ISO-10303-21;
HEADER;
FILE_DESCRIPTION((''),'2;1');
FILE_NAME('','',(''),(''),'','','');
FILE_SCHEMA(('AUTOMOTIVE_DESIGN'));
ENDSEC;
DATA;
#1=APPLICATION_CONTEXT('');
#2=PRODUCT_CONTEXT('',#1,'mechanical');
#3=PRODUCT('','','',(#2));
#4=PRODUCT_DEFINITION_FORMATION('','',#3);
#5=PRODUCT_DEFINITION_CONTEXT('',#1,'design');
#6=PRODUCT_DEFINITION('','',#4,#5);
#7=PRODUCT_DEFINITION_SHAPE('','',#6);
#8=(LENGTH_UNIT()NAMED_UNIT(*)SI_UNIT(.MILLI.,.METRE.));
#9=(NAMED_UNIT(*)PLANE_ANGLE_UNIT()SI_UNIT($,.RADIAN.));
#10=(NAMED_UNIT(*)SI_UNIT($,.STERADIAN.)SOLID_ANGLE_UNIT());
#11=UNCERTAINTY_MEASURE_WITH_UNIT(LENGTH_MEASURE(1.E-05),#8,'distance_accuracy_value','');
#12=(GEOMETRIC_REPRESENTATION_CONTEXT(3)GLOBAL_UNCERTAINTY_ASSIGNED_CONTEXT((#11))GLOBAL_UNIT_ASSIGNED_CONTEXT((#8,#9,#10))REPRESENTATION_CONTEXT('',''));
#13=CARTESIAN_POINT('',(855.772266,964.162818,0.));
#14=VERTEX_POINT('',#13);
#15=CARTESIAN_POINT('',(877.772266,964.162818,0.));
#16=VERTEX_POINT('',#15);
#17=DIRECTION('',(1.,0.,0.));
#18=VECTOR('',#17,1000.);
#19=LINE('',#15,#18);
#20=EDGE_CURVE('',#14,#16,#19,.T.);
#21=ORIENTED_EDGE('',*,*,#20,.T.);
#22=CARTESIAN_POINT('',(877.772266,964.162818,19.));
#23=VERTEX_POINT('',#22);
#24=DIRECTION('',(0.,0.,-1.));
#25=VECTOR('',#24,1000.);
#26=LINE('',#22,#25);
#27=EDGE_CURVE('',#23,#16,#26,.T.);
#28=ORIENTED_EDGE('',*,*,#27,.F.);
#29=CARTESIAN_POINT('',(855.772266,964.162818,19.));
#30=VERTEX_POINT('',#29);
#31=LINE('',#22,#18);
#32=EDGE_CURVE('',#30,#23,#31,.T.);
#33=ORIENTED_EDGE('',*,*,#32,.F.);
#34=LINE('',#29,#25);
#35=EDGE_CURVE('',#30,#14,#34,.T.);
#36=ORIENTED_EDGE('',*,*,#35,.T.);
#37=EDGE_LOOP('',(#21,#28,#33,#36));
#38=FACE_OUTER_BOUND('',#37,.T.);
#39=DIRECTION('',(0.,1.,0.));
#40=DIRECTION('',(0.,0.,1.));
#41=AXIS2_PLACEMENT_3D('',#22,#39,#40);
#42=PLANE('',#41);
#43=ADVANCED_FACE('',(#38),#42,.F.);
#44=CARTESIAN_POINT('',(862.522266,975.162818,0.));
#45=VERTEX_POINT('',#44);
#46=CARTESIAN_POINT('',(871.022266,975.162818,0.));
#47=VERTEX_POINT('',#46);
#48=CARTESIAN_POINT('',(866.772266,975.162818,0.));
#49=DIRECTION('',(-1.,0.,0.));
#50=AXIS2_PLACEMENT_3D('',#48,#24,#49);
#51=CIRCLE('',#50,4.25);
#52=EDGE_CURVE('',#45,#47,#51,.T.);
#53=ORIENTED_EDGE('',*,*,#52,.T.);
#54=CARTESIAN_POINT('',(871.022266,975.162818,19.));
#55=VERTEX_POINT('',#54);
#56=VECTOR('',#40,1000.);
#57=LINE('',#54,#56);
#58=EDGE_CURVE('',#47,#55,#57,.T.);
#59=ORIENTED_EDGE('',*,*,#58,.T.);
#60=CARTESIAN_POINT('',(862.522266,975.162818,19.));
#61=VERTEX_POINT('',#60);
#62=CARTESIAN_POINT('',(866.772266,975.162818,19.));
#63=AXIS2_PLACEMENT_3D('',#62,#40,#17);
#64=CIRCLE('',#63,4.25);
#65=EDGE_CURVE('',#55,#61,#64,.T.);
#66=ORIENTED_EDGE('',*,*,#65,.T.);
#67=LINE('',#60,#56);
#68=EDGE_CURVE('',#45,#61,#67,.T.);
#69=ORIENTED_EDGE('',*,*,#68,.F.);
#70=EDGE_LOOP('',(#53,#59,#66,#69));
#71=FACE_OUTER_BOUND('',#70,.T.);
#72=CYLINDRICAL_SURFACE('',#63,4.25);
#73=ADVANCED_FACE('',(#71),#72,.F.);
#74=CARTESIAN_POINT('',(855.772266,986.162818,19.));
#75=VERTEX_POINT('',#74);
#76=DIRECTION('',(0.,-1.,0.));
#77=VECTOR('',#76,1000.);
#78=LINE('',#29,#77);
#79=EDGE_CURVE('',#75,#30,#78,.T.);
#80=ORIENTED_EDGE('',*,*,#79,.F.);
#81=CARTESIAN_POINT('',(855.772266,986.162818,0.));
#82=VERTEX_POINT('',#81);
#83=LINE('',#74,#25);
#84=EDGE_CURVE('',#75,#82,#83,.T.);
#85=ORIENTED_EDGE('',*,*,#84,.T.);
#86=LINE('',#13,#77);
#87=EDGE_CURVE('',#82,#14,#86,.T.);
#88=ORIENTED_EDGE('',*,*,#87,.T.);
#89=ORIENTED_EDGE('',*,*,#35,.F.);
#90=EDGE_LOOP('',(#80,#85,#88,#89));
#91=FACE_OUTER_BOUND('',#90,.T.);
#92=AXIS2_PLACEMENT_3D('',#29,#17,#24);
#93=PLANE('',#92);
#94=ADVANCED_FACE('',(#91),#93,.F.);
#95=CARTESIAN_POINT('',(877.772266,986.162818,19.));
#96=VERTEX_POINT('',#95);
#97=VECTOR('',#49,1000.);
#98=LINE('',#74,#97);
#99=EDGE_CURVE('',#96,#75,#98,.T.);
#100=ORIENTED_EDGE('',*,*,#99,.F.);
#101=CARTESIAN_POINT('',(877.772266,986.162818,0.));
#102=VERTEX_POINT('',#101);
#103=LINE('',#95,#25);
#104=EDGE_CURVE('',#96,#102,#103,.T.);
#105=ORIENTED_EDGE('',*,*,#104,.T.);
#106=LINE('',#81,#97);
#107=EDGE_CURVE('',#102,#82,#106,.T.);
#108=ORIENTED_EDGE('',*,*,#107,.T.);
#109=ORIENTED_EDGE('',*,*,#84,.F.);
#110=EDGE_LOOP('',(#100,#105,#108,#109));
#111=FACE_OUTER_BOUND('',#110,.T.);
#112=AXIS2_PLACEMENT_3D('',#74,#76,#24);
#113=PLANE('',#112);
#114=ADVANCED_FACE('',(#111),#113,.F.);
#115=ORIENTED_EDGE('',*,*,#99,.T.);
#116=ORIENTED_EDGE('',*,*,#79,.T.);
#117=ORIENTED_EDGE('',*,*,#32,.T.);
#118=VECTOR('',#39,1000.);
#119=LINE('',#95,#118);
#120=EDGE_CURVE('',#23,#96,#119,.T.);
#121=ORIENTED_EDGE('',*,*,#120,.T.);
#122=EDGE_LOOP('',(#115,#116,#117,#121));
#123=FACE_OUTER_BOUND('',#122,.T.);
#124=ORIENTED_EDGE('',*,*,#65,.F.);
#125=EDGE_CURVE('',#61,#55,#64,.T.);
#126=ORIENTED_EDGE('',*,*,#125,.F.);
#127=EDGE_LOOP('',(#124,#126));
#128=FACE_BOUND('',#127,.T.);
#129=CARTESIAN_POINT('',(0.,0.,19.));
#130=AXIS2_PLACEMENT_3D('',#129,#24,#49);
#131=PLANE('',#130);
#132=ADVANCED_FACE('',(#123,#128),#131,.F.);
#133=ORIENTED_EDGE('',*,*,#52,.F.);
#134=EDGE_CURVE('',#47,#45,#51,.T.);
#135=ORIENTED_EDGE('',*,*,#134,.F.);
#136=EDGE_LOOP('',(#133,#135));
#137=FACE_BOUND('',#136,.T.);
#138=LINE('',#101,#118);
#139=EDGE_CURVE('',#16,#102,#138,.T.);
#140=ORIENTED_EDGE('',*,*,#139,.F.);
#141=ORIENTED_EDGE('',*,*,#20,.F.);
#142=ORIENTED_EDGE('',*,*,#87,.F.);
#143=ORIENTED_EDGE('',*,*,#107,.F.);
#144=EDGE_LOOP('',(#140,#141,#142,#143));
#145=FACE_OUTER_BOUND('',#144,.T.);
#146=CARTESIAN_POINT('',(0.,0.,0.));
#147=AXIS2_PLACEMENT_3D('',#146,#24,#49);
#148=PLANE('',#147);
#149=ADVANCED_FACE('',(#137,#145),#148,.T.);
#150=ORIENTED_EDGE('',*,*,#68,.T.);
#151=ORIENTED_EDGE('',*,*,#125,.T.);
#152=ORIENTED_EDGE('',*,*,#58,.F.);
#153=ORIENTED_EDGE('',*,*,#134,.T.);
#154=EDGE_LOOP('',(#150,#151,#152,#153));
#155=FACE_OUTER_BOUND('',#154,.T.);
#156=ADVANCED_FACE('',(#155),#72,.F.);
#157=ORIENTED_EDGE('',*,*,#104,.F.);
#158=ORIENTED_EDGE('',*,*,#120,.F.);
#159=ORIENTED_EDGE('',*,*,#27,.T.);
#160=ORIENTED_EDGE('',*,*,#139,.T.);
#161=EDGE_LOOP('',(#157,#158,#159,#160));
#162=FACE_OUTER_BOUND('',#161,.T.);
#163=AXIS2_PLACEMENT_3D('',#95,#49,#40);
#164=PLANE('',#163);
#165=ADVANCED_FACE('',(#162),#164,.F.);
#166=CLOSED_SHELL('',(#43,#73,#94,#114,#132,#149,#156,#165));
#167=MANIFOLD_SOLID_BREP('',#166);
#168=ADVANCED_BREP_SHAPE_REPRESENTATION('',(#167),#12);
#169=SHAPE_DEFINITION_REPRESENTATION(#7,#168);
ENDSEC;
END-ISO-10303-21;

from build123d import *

# Parameters (mm, degrees)
SKETCH1_W              = 22
SKETCH1_H              = 22
SKETCH1_R              = 4
BOSS_EXTRUDE1_DEPTH    = 19
M10_TAPPED_HOLE2_D     = 8.5
M10_TAPPED_HOLE2_DEPTH = 27.5
M10_TAPPED_HOLE2_TIP   = 2.553657631


with BuildPart() as part:
    # Sketch1 → Boss-Extrude1 (new body)
    with BuildSketch(Plane.XY):
        with Locations((866.772265526, 975.162817643)):
            Rectangle(SKETCH1_W, SKETCH1_H)
        with Locations((866.772265526, 975.162817643)):
            Circle(SKETCH1_R, mode=Mode.SUBTRACT)
    extrude(amount=BOSS_EXTRUDE1_DEPTH)

    # M10 Tapped Hole2
    with Locations(Plane(origin=(866.772265526, 975.162817643, 19), x_dir=(1, 0, 0), z_dir=(0, 0, 1))):
        with Locations((0, 0)):
            Hole(M10_TAPPED_HOLE2_D / 2, depth=M10_TAPPED_HOLE2_DEPTH)
            with Locations((0, 0, -(M10_TAPPED_HOLE2_DEPTH + M10_TAPPED_HOLE2_TIP / 2))):  # 118° drill point
                Cone(0, M10_TAPPED_HOLE2_D / 2, M10_TAPPED_HOLE2_TIP, mode=Mode.SUBTRACT)


solid = part.part
